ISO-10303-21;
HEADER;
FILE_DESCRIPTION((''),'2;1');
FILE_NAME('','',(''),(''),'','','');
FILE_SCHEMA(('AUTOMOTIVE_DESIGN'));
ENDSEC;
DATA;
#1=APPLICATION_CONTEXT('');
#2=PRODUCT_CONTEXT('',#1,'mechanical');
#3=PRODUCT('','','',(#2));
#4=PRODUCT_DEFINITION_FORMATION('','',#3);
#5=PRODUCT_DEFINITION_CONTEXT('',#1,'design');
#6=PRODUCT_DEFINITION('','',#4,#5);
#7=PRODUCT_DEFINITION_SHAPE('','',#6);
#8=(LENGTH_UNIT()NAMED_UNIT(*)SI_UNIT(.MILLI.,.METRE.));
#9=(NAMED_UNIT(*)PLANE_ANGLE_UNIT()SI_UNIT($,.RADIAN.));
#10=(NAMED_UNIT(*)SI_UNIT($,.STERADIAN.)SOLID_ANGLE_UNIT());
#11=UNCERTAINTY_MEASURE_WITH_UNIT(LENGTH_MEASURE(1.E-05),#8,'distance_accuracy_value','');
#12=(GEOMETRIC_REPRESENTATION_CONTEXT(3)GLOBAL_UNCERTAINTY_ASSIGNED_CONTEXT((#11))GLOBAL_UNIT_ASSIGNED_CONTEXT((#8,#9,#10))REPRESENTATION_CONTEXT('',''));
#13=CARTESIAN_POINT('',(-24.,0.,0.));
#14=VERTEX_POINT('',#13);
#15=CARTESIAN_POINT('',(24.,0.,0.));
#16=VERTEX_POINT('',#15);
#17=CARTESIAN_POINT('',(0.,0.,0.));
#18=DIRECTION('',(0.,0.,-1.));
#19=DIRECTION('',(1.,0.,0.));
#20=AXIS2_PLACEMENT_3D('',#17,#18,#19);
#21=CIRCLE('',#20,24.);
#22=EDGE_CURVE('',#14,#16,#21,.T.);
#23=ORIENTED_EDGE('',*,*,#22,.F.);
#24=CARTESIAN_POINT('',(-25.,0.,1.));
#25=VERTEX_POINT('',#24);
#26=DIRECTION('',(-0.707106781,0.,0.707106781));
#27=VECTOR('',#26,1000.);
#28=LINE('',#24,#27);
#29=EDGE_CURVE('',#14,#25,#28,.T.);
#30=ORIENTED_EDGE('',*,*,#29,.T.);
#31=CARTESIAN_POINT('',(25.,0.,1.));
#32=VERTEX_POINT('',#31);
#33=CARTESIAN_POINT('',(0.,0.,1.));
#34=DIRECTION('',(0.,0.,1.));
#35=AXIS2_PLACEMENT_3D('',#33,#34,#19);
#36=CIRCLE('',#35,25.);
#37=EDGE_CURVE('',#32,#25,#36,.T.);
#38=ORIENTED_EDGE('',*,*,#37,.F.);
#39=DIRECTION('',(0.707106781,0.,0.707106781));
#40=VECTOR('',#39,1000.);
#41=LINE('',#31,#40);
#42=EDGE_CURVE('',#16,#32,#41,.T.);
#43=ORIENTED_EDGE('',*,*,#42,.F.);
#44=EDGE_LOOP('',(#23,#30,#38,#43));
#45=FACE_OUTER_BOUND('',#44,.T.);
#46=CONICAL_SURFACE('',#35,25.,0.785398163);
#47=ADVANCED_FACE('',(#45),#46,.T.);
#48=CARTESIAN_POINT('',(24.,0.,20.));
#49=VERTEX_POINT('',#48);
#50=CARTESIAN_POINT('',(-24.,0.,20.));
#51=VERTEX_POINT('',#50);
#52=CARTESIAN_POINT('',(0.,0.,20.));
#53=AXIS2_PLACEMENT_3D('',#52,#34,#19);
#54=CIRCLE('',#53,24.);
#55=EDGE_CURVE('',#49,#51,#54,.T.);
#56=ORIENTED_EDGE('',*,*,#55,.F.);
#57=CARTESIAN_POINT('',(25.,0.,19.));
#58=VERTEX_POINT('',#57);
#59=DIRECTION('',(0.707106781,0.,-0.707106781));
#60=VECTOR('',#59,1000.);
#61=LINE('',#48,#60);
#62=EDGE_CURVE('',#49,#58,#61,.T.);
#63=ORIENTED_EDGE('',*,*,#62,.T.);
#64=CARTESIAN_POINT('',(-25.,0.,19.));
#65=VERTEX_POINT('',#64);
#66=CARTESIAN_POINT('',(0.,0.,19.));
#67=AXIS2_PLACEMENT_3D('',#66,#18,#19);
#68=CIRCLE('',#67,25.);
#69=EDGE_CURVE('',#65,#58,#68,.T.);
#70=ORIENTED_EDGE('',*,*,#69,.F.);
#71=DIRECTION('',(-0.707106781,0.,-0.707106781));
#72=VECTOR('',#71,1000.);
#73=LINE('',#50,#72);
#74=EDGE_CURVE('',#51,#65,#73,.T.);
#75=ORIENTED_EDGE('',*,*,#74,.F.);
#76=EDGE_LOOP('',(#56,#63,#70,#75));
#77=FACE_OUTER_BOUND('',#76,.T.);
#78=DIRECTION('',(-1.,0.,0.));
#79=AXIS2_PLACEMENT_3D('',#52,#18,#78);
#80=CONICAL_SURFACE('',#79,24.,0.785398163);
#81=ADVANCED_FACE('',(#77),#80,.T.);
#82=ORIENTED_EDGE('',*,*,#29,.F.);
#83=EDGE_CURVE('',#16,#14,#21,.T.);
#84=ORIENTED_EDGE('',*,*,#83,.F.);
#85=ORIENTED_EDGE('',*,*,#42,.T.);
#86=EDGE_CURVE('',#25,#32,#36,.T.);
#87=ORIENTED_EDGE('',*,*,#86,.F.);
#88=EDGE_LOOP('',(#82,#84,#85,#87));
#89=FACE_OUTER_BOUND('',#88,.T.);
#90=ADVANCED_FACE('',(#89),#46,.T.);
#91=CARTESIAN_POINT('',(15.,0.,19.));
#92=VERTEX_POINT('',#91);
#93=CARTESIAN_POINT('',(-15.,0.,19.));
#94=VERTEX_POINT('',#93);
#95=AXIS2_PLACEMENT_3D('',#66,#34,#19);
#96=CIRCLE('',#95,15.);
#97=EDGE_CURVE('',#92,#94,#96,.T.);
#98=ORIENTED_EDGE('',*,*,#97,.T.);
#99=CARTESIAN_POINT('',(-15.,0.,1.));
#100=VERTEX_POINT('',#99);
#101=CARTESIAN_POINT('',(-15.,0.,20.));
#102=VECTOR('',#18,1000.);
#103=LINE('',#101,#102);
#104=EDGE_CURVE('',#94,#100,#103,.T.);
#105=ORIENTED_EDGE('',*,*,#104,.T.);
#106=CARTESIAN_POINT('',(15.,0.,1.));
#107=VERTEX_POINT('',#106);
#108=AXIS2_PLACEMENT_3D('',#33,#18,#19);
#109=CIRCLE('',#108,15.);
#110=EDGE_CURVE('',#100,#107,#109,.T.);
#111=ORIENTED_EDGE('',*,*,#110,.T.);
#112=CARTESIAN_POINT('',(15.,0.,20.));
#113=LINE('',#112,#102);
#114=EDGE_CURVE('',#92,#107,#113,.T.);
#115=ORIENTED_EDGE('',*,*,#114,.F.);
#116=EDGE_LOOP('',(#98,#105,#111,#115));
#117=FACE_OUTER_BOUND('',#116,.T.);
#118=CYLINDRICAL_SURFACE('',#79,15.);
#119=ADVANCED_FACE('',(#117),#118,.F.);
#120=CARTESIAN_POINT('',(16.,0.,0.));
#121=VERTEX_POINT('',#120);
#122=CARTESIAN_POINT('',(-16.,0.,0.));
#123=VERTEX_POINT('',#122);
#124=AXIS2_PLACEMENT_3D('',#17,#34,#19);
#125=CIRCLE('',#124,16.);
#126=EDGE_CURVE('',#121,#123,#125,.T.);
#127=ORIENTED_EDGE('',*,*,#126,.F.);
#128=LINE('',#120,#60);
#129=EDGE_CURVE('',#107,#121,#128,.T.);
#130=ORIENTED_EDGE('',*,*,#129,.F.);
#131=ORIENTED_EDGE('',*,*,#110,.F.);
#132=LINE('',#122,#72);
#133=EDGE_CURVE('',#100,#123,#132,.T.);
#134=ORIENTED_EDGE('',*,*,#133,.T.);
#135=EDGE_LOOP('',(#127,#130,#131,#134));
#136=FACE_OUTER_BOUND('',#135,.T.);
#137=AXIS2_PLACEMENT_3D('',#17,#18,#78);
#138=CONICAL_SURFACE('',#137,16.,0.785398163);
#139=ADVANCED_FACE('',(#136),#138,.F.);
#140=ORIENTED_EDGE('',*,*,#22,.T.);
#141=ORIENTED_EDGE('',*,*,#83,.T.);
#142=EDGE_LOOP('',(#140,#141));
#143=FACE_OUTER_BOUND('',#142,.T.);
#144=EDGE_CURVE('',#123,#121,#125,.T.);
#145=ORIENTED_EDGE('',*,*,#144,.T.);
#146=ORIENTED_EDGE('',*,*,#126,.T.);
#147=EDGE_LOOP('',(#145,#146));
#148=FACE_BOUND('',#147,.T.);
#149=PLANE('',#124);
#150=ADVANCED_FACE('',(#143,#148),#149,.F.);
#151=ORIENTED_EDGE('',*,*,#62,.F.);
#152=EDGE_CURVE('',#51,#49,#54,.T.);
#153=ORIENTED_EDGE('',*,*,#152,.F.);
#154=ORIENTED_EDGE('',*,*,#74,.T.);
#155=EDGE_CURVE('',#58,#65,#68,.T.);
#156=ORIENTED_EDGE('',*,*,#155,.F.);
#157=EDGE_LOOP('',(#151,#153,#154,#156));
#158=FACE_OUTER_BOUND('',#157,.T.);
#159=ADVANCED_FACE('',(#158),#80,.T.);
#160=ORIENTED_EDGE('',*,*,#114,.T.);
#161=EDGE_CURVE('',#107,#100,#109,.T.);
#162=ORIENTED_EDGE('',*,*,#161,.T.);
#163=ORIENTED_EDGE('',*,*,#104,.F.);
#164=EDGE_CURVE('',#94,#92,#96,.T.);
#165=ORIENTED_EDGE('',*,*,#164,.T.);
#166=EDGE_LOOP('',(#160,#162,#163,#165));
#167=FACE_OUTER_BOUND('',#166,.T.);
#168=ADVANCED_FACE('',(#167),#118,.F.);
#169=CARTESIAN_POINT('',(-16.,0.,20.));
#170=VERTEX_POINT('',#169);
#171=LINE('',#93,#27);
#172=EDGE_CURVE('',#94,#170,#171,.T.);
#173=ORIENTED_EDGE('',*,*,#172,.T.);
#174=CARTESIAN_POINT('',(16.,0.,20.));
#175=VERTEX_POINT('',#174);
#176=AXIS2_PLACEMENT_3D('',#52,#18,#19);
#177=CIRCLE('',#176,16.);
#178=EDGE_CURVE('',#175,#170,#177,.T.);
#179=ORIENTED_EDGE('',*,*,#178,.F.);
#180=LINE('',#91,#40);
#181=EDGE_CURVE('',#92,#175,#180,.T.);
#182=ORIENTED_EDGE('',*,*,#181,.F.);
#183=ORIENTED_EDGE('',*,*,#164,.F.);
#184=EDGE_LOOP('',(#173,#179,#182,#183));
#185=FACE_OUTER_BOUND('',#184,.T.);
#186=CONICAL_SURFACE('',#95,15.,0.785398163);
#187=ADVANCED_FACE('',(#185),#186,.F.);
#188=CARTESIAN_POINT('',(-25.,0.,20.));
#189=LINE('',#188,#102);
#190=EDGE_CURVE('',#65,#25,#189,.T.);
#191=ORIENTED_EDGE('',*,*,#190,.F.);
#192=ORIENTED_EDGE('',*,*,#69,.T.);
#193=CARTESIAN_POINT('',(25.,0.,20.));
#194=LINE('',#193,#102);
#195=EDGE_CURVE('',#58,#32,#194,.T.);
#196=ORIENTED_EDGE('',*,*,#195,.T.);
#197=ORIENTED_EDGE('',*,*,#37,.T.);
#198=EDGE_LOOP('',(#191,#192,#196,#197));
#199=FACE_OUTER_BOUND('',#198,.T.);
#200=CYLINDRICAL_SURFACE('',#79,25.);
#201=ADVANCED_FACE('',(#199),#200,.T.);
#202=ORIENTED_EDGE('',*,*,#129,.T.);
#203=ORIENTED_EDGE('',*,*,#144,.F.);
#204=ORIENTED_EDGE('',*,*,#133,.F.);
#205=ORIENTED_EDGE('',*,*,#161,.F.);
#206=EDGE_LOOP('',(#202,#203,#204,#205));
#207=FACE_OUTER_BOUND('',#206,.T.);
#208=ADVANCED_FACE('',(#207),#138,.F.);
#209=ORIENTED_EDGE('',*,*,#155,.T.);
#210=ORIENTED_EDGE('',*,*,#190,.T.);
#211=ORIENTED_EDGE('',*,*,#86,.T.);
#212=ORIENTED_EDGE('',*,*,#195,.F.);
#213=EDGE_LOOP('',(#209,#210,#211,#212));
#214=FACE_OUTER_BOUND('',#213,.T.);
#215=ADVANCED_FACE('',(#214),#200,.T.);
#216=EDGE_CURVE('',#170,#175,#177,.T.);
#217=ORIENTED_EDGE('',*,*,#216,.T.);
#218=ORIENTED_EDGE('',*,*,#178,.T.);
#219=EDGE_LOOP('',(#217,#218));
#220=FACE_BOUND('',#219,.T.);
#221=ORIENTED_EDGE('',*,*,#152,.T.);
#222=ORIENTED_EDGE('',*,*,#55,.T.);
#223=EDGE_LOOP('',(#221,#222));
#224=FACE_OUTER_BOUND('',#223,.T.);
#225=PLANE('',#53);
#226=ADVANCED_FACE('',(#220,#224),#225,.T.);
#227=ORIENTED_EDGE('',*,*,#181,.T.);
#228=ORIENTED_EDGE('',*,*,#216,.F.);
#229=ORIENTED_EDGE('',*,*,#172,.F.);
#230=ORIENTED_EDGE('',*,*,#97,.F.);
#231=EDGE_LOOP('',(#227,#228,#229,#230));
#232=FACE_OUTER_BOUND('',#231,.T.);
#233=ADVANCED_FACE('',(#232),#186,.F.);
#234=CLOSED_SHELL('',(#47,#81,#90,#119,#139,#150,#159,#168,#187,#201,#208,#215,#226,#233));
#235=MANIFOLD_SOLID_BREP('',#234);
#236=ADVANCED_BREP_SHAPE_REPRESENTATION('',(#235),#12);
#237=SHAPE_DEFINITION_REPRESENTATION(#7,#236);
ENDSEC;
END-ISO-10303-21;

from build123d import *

# Parameters (mm, degrees)
SKETCH1_R           = 25
SKETCH1_R_2         = 15
BOSS_EXTRUDE1_DEPTH = 20
CHAMFER1_SIZE       = 1


with BuildPart() as part:
    # Sketch1 → Boss-Extrude1 (new body)
    with BuildSketch(Plane.XY):
        Circle(SKETCH1_R)
        Circle(SKETCH1_R_2, mode=Mode.SUBTRACT)
    extrude(amount=BOSS_EXTRUDE1_DEPTH)

    # Chamfer1
    chamfer1_edges = [part.edges().sort_by_distance(p)[0] for p in [
        (-25, 0, 0),
        (-25, 0, 20),
        (-15, 0, 0),
        (-15, 0, 20),
    ]]
    chamfer(chamfer1_edges, length=CHAMFER1_SIZE)


solid = part.part
